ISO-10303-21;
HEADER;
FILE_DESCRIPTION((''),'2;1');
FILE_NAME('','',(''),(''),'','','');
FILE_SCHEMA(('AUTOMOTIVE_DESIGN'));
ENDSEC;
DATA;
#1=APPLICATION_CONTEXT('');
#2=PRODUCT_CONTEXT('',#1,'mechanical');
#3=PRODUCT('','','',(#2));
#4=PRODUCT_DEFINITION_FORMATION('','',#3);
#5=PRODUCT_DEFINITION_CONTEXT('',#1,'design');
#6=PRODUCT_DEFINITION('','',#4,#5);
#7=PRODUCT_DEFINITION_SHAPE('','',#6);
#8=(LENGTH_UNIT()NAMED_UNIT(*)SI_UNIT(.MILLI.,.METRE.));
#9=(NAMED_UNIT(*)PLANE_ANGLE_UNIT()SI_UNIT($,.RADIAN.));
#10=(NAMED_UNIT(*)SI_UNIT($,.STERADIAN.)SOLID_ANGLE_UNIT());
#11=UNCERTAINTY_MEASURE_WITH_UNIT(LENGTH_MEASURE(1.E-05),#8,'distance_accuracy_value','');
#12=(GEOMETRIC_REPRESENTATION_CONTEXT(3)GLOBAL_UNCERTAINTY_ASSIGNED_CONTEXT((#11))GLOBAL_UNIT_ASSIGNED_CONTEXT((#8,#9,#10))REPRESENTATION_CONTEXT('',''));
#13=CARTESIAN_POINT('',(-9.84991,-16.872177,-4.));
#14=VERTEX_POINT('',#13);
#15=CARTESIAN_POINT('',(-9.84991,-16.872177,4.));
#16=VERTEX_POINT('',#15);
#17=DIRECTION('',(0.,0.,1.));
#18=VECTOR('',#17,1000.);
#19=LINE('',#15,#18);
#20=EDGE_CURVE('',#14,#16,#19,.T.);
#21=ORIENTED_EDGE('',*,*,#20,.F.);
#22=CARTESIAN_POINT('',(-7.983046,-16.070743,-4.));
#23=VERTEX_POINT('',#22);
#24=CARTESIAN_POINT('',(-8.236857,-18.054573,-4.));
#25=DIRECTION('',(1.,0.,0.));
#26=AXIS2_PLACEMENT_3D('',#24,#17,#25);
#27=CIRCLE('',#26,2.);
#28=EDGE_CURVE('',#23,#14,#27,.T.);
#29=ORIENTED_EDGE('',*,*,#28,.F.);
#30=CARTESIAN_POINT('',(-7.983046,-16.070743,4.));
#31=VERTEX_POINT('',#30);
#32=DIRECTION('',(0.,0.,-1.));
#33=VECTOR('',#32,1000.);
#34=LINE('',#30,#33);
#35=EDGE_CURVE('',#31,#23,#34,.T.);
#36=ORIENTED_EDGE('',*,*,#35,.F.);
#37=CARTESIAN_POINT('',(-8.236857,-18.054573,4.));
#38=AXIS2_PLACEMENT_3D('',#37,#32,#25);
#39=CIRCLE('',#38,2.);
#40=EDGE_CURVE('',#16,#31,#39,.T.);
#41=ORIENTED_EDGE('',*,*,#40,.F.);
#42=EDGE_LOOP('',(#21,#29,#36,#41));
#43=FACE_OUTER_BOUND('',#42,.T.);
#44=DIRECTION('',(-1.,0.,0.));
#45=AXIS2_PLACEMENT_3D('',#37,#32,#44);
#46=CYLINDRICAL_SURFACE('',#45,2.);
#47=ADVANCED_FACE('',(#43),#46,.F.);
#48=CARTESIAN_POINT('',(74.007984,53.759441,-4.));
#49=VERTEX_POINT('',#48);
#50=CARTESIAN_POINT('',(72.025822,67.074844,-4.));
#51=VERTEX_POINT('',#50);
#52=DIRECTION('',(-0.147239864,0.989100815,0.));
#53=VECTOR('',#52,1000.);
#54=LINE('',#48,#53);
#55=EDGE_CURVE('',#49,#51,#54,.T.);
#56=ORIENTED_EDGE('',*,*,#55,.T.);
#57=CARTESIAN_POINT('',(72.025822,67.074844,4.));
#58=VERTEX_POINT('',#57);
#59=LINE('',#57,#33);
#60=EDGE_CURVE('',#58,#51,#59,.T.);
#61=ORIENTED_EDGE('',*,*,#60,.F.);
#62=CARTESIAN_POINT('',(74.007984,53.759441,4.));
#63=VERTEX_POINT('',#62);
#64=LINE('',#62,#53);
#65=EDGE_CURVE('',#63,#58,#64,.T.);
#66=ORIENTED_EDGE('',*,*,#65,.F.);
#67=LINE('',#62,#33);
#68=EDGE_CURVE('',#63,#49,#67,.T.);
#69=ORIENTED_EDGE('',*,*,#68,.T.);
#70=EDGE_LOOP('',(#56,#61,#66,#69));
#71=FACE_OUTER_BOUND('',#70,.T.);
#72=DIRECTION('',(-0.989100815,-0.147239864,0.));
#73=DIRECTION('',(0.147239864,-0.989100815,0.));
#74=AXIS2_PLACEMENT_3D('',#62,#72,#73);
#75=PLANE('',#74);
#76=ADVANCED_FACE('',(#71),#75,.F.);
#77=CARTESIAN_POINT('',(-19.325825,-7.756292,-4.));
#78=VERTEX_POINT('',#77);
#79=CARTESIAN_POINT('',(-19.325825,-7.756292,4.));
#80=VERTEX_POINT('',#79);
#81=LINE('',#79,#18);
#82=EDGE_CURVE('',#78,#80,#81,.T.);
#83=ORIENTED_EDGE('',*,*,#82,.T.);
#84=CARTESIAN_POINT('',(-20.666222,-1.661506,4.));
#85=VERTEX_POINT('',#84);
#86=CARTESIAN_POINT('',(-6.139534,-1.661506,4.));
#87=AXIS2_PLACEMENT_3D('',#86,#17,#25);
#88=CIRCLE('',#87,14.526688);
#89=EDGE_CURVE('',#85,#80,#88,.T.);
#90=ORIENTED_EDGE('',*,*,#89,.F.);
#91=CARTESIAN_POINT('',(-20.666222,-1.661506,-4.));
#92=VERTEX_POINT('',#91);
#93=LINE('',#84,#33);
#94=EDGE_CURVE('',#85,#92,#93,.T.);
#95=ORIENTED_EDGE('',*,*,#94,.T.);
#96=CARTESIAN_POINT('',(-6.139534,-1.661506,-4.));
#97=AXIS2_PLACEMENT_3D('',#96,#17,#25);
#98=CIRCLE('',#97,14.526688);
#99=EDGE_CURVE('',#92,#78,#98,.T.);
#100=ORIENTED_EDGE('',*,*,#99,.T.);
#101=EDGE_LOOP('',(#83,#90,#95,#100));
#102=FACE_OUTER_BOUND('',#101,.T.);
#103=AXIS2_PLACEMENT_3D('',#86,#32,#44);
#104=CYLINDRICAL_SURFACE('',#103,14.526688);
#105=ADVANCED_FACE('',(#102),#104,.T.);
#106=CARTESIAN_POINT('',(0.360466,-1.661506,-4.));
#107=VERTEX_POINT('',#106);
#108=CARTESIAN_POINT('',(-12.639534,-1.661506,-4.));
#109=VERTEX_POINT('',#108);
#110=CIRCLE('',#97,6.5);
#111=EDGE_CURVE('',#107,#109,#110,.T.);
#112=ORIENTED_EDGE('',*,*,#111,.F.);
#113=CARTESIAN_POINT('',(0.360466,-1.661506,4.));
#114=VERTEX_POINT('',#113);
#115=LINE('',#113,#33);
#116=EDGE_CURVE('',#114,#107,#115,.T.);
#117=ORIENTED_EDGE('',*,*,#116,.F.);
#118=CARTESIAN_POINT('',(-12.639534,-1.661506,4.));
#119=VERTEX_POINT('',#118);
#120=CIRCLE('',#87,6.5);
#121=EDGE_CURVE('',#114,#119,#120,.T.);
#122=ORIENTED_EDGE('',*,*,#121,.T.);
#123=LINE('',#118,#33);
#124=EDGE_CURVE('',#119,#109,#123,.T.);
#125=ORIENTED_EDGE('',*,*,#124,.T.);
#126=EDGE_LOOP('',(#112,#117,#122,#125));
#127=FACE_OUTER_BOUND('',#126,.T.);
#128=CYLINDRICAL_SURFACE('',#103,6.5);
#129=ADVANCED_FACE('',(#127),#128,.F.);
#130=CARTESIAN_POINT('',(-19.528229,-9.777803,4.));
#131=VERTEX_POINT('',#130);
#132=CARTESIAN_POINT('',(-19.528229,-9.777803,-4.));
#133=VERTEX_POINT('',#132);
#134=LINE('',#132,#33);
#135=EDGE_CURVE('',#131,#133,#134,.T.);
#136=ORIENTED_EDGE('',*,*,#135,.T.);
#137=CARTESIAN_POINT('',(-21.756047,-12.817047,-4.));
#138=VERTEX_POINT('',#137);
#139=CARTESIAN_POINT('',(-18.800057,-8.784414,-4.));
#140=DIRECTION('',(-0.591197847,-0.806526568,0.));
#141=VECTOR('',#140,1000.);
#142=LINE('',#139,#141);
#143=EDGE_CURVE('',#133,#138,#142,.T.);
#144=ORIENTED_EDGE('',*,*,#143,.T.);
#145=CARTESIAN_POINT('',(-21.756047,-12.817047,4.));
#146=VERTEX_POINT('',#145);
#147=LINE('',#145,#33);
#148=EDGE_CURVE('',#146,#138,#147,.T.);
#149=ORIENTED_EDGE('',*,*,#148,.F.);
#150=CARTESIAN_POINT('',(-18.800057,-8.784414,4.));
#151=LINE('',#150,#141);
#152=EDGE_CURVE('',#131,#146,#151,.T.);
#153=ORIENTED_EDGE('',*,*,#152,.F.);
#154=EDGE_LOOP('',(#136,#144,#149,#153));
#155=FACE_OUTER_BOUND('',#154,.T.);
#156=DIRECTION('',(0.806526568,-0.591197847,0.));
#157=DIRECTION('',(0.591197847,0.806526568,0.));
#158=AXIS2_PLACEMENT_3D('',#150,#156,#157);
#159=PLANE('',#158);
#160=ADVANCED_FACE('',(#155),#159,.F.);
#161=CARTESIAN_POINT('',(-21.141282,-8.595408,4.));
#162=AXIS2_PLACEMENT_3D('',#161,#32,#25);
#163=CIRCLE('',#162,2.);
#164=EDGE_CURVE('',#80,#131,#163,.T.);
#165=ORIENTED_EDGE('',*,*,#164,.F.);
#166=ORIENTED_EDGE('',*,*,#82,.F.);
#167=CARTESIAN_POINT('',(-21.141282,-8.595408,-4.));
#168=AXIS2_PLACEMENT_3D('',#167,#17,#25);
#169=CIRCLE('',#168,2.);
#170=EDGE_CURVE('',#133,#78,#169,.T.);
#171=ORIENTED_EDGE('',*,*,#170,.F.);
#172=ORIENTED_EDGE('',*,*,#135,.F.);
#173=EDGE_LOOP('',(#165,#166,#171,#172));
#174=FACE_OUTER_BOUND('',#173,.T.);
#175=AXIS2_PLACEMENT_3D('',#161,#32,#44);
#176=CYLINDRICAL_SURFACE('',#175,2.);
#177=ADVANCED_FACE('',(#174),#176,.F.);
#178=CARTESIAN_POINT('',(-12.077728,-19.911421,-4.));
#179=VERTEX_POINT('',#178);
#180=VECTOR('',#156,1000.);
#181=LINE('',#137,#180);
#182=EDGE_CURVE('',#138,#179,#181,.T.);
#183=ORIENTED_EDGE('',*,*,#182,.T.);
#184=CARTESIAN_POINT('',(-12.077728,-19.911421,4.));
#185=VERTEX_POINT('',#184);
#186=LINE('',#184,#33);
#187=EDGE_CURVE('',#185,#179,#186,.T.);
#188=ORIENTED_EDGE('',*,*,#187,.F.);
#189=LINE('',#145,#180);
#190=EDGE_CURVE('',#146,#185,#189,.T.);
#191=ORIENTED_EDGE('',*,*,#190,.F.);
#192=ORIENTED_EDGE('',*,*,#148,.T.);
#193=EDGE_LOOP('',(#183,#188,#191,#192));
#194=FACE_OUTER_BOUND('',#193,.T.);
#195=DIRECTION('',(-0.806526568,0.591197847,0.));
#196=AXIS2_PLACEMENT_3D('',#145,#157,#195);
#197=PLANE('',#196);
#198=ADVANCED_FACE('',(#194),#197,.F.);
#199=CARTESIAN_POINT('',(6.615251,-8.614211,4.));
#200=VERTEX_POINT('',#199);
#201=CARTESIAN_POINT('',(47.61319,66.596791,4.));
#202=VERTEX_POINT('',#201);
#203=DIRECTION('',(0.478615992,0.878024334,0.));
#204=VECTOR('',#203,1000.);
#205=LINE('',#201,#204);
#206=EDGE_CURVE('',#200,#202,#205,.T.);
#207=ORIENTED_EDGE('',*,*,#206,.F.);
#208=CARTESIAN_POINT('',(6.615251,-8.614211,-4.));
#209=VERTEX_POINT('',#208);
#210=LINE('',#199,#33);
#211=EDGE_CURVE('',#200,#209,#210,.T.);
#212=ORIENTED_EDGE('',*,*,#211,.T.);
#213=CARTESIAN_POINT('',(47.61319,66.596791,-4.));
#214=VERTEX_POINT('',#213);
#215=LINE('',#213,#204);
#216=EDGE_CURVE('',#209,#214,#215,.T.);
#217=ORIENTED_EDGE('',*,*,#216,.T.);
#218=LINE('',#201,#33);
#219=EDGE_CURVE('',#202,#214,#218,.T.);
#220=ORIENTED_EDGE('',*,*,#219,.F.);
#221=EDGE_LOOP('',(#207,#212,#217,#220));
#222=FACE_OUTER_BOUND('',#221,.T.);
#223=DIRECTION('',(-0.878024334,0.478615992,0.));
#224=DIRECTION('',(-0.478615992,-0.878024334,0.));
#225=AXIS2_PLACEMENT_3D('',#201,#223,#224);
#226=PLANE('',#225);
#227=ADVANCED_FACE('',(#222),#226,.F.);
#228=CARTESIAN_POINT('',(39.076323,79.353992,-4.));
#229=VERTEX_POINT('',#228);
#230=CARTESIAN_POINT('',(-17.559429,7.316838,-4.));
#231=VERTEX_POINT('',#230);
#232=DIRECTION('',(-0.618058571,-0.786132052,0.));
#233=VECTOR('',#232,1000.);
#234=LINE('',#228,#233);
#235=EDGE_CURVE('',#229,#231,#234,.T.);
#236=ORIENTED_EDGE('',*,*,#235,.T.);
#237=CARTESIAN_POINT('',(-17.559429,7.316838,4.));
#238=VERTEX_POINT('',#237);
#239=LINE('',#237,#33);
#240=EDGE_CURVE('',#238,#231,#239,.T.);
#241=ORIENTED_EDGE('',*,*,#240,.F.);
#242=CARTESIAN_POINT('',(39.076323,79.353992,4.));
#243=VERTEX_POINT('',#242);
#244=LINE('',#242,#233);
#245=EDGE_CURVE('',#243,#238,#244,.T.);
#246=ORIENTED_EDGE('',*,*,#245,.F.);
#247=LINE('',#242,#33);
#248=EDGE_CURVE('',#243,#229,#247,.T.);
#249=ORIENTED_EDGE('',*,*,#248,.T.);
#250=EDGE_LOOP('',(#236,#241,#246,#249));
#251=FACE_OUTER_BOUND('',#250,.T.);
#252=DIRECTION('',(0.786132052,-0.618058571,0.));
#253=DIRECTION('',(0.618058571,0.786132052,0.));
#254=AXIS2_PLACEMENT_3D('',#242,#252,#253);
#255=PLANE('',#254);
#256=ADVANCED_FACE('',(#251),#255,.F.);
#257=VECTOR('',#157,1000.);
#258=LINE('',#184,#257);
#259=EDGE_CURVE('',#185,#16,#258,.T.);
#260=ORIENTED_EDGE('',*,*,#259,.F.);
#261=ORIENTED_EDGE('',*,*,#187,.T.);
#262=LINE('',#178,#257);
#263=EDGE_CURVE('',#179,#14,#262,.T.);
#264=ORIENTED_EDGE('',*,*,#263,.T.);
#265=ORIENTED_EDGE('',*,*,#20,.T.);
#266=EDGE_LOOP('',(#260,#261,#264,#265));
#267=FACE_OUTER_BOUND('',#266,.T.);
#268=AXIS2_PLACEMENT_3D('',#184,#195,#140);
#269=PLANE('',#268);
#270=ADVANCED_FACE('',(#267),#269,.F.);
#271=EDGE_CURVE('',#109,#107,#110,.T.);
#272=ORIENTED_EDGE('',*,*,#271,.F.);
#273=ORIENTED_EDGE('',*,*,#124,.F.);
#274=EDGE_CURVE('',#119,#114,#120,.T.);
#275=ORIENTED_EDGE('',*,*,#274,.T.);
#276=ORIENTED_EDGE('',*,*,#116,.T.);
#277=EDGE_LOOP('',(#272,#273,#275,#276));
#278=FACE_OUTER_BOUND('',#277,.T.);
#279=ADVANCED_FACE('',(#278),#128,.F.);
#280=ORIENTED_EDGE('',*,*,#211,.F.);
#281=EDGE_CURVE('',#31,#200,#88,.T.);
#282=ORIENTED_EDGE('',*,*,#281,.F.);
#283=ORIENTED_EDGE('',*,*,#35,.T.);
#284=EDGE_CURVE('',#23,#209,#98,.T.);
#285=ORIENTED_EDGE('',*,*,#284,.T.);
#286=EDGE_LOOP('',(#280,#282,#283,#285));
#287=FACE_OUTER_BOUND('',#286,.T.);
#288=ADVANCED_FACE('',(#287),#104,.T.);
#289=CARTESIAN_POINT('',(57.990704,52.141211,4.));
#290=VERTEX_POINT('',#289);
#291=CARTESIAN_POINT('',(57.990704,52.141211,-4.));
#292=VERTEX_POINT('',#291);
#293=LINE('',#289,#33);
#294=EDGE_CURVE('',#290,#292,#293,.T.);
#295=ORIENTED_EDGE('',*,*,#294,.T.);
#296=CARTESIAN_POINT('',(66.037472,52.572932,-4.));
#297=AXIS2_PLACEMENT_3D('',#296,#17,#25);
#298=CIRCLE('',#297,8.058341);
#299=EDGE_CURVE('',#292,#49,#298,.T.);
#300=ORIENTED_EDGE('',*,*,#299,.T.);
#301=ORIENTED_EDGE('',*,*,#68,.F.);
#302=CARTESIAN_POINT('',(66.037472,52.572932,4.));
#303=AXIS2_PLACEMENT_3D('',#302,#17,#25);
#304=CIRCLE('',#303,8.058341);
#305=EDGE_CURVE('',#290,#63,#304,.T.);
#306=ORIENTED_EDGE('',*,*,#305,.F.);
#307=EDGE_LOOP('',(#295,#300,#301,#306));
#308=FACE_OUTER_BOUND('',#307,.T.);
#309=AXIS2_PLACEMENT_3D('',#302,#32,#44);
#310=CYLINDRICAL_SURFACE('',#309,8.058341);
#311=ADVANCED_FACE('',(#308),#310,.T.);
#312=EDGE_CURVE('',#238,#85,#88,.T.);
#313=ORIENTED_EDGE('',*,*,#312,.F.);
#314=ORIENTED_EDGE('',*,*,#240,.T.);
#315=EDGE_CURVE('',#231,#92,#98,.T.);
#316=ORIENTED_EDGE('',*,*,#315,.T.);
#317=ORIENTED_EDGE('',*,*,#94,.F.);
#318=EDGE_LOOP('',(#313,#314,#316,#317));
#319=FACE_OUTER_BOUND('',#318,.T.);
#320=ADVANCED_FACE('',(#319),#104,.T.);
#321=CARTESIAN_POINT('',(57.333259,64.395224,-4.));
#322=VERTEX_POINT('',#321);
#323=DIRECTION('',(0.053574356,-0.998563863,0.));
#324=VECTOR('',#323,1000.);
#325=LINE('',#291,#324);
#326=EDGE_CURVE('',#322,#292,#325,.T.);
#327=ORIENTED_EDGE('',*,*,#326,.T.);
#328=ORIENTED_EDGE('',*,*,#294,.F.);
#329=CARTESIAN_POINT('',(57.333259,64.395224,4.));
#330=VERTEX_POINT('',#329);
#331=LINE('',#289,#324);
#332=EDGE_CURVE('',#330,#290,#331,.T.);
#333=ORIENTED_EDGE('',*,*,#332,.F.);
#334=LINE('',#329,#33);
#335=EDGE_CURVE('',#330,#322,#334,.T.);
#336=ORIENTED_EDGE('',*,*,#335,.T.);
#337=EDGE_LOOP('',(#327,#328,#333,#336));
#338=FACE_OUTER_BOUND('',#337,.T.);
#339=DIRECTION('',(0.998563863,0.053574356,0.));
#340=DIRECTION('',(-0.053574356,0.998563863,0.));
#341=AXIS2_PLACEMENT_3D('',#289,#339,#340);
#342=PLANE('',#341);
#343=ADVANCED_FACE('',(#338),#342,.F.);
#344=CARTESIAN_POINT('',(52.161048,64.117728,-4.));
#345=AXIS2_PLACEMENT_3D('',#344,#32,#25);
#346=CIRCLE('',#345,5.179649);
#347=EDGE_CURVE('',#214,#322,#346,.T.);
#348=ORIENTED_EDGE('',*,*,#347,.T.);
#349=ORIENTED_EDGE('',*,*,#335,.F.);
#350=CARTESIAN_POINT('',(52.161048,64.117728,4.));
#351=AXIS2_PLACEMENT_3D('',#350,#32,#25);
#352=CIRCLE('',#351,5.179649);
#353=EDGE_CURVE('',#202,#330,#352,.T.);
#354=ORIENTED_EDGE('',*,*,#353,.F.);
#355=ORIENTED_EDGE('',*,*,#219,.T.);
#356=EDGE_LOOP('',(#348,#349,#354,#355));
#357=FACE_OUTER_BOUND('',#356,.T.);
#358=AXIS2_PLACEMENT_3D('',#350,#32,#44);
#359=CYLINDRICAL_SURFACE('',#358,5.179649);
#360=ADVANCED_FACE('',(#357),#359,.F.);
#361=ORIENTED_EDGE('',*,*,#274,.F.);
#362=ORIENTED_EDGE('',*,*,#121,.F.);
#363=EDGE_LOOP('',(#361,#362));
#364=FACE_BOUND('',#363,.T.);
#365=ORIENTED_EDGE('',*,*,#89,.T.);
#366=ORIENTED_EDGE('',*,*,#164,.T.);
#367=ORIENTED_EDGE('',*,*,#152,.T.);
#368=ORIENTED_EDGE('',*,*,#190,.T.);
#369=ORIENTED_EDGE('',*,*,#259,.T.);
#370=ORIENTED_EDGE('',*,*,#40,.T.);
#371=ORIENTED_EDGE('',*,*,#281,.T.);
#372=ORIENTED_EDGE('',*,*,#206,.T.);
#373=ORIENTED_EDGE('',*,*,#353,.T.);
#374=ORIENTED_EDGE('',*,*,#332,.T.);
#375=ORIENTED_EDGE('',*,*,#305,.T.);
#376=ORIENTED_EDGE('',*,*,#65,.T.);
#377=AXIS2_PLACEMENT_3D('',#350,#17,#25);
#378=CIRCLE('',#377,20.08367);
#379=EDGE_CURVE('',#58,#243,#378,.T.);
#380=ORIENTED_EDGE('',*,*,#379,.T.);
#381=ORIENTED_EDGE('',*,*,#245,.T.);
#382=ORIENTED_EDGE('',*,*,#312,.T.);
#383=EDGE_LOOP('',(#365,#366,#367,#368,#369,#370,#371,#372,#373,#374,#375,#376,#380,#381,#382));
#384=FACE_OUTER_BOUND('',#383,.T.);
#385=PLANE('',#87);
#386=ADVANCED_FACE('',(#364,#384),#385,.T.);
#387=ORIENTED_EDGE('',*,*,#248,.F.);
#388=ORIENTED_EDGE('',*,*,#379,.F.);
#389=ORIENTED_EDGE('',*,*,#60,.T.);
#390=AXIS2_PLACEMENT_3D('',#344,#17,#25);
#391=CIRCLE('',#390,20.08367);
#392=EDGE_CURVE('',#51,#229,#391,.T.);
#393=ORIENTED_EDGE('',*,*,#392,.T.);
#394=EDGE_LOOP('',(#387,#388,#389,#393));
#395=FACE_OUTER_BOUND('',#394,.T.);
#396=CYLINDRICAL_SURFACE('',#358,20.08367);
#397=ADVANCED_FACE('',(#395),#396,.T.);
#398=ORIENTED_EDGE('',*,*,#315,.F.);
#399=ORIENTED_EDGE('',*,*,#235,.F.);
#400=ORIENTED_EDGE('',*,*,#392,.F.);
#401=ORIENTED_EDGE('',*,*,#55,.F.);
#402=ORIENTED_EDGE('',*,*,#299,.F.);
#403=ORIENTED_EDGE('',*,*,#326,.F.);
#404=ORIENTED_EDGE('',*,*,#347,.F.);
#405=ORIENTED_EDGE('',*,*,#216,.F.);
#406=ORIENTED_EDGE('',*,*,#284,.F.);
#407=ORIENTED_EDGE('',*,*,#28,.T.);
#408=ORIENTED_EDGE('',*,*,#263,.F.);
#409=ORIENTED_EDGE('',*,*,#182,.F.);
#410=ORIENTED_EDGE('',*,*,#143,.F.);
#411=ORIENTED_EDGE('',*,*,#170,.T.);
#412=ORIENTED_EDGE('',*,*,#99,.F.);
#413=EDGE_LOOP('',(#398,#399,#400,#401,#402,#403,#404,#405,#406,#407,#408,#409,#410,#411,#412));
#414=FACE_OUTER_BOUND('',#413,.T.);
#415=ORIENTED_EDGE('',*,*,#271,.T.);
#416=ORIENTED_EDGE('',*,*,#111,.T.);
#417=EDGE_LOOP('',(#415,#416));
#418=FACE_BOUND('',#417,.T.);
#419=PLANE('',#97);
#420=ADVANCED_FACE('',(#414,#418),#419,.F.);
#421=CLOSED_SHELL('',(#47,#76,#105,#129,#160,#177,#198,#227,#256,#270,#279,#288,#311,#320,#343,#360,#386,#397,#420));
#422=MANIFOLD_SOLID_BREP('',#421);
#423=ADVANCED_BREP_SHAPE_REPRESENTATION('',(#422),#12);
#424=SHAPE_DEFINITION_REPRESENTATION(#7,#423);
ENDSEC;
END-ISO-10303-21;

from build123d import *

# Parameters (mm, degrees)
SKETCH1_R           = 6.5
BOSS_EXTRUDE1_DEPTH = 4
FILLET1_R           = 2


with BuildPart() as part:
    # Sketch1 → Boss-Extrude1 (new, symmetric)
    with BuildSketch(Plane.XY):
        with BuildLine():
            Line((47.613190214, 66.596790509), (6.61525122, -8.614210923))
            ThreePointArc((6.61525122, -8.614210923), (-0.051073307, -14.850717485), (-9.121738509, -15.878788295))
            Line((-9.121738509, -15.878788295), (-12.077727744, -19.911421137))
            Line((-12.077727744, -19.911421137), (-21.756046565, -12.817046972))
            Line((-21.756046565, -12.817046972), (-18.80005733, -8.784414129))
            ThreePointArc((-18.80005733, -8.784414129), (-20.623291354, -0.545508517), (-17.559429464, 7.316838354))
            Line((-17.559429464, 7.316838354), (39.076322986, 79.353992026))
            ThreePointArc((39.076322986, 79.353992026), (59.174366459, 82.937056923), (72.02582234, 67.074844364))
            Line((72.02582234, 67.074844364), (74.007984491, 53.75944084))
            ThreePointArc((74.007984491, 53.75944084), (66.847485005, 44.555404253), (57.99070376, 52.141211286))
            Line((57.99070376, 52.141211286), (57.333258746, 64.39522394))
            ThreePointArc((57.333258746, 64.39522394), (53.305241341, 69.169419157), (47.613190214, 66.596790509))
        make_face()
        with Locations((-6.139534384, -1.661505705)):
            Circle(SKETCH1_R, mode=Mode.SUBTRACT)
    extrude(amount=BOSS_EXTRUDE1_DEPTH, both=True)

    # Fillet1
    fillet1_edges = [part.edges().sort_by_distance(p)[0] for p in [
        (-18.80005733, -8.784414129, 0),
        (-9.121738509, -15.878788295, 0),
    ]]
    fillet(fillet1_edges, radius=FILLET1_R)


solid = part.part
